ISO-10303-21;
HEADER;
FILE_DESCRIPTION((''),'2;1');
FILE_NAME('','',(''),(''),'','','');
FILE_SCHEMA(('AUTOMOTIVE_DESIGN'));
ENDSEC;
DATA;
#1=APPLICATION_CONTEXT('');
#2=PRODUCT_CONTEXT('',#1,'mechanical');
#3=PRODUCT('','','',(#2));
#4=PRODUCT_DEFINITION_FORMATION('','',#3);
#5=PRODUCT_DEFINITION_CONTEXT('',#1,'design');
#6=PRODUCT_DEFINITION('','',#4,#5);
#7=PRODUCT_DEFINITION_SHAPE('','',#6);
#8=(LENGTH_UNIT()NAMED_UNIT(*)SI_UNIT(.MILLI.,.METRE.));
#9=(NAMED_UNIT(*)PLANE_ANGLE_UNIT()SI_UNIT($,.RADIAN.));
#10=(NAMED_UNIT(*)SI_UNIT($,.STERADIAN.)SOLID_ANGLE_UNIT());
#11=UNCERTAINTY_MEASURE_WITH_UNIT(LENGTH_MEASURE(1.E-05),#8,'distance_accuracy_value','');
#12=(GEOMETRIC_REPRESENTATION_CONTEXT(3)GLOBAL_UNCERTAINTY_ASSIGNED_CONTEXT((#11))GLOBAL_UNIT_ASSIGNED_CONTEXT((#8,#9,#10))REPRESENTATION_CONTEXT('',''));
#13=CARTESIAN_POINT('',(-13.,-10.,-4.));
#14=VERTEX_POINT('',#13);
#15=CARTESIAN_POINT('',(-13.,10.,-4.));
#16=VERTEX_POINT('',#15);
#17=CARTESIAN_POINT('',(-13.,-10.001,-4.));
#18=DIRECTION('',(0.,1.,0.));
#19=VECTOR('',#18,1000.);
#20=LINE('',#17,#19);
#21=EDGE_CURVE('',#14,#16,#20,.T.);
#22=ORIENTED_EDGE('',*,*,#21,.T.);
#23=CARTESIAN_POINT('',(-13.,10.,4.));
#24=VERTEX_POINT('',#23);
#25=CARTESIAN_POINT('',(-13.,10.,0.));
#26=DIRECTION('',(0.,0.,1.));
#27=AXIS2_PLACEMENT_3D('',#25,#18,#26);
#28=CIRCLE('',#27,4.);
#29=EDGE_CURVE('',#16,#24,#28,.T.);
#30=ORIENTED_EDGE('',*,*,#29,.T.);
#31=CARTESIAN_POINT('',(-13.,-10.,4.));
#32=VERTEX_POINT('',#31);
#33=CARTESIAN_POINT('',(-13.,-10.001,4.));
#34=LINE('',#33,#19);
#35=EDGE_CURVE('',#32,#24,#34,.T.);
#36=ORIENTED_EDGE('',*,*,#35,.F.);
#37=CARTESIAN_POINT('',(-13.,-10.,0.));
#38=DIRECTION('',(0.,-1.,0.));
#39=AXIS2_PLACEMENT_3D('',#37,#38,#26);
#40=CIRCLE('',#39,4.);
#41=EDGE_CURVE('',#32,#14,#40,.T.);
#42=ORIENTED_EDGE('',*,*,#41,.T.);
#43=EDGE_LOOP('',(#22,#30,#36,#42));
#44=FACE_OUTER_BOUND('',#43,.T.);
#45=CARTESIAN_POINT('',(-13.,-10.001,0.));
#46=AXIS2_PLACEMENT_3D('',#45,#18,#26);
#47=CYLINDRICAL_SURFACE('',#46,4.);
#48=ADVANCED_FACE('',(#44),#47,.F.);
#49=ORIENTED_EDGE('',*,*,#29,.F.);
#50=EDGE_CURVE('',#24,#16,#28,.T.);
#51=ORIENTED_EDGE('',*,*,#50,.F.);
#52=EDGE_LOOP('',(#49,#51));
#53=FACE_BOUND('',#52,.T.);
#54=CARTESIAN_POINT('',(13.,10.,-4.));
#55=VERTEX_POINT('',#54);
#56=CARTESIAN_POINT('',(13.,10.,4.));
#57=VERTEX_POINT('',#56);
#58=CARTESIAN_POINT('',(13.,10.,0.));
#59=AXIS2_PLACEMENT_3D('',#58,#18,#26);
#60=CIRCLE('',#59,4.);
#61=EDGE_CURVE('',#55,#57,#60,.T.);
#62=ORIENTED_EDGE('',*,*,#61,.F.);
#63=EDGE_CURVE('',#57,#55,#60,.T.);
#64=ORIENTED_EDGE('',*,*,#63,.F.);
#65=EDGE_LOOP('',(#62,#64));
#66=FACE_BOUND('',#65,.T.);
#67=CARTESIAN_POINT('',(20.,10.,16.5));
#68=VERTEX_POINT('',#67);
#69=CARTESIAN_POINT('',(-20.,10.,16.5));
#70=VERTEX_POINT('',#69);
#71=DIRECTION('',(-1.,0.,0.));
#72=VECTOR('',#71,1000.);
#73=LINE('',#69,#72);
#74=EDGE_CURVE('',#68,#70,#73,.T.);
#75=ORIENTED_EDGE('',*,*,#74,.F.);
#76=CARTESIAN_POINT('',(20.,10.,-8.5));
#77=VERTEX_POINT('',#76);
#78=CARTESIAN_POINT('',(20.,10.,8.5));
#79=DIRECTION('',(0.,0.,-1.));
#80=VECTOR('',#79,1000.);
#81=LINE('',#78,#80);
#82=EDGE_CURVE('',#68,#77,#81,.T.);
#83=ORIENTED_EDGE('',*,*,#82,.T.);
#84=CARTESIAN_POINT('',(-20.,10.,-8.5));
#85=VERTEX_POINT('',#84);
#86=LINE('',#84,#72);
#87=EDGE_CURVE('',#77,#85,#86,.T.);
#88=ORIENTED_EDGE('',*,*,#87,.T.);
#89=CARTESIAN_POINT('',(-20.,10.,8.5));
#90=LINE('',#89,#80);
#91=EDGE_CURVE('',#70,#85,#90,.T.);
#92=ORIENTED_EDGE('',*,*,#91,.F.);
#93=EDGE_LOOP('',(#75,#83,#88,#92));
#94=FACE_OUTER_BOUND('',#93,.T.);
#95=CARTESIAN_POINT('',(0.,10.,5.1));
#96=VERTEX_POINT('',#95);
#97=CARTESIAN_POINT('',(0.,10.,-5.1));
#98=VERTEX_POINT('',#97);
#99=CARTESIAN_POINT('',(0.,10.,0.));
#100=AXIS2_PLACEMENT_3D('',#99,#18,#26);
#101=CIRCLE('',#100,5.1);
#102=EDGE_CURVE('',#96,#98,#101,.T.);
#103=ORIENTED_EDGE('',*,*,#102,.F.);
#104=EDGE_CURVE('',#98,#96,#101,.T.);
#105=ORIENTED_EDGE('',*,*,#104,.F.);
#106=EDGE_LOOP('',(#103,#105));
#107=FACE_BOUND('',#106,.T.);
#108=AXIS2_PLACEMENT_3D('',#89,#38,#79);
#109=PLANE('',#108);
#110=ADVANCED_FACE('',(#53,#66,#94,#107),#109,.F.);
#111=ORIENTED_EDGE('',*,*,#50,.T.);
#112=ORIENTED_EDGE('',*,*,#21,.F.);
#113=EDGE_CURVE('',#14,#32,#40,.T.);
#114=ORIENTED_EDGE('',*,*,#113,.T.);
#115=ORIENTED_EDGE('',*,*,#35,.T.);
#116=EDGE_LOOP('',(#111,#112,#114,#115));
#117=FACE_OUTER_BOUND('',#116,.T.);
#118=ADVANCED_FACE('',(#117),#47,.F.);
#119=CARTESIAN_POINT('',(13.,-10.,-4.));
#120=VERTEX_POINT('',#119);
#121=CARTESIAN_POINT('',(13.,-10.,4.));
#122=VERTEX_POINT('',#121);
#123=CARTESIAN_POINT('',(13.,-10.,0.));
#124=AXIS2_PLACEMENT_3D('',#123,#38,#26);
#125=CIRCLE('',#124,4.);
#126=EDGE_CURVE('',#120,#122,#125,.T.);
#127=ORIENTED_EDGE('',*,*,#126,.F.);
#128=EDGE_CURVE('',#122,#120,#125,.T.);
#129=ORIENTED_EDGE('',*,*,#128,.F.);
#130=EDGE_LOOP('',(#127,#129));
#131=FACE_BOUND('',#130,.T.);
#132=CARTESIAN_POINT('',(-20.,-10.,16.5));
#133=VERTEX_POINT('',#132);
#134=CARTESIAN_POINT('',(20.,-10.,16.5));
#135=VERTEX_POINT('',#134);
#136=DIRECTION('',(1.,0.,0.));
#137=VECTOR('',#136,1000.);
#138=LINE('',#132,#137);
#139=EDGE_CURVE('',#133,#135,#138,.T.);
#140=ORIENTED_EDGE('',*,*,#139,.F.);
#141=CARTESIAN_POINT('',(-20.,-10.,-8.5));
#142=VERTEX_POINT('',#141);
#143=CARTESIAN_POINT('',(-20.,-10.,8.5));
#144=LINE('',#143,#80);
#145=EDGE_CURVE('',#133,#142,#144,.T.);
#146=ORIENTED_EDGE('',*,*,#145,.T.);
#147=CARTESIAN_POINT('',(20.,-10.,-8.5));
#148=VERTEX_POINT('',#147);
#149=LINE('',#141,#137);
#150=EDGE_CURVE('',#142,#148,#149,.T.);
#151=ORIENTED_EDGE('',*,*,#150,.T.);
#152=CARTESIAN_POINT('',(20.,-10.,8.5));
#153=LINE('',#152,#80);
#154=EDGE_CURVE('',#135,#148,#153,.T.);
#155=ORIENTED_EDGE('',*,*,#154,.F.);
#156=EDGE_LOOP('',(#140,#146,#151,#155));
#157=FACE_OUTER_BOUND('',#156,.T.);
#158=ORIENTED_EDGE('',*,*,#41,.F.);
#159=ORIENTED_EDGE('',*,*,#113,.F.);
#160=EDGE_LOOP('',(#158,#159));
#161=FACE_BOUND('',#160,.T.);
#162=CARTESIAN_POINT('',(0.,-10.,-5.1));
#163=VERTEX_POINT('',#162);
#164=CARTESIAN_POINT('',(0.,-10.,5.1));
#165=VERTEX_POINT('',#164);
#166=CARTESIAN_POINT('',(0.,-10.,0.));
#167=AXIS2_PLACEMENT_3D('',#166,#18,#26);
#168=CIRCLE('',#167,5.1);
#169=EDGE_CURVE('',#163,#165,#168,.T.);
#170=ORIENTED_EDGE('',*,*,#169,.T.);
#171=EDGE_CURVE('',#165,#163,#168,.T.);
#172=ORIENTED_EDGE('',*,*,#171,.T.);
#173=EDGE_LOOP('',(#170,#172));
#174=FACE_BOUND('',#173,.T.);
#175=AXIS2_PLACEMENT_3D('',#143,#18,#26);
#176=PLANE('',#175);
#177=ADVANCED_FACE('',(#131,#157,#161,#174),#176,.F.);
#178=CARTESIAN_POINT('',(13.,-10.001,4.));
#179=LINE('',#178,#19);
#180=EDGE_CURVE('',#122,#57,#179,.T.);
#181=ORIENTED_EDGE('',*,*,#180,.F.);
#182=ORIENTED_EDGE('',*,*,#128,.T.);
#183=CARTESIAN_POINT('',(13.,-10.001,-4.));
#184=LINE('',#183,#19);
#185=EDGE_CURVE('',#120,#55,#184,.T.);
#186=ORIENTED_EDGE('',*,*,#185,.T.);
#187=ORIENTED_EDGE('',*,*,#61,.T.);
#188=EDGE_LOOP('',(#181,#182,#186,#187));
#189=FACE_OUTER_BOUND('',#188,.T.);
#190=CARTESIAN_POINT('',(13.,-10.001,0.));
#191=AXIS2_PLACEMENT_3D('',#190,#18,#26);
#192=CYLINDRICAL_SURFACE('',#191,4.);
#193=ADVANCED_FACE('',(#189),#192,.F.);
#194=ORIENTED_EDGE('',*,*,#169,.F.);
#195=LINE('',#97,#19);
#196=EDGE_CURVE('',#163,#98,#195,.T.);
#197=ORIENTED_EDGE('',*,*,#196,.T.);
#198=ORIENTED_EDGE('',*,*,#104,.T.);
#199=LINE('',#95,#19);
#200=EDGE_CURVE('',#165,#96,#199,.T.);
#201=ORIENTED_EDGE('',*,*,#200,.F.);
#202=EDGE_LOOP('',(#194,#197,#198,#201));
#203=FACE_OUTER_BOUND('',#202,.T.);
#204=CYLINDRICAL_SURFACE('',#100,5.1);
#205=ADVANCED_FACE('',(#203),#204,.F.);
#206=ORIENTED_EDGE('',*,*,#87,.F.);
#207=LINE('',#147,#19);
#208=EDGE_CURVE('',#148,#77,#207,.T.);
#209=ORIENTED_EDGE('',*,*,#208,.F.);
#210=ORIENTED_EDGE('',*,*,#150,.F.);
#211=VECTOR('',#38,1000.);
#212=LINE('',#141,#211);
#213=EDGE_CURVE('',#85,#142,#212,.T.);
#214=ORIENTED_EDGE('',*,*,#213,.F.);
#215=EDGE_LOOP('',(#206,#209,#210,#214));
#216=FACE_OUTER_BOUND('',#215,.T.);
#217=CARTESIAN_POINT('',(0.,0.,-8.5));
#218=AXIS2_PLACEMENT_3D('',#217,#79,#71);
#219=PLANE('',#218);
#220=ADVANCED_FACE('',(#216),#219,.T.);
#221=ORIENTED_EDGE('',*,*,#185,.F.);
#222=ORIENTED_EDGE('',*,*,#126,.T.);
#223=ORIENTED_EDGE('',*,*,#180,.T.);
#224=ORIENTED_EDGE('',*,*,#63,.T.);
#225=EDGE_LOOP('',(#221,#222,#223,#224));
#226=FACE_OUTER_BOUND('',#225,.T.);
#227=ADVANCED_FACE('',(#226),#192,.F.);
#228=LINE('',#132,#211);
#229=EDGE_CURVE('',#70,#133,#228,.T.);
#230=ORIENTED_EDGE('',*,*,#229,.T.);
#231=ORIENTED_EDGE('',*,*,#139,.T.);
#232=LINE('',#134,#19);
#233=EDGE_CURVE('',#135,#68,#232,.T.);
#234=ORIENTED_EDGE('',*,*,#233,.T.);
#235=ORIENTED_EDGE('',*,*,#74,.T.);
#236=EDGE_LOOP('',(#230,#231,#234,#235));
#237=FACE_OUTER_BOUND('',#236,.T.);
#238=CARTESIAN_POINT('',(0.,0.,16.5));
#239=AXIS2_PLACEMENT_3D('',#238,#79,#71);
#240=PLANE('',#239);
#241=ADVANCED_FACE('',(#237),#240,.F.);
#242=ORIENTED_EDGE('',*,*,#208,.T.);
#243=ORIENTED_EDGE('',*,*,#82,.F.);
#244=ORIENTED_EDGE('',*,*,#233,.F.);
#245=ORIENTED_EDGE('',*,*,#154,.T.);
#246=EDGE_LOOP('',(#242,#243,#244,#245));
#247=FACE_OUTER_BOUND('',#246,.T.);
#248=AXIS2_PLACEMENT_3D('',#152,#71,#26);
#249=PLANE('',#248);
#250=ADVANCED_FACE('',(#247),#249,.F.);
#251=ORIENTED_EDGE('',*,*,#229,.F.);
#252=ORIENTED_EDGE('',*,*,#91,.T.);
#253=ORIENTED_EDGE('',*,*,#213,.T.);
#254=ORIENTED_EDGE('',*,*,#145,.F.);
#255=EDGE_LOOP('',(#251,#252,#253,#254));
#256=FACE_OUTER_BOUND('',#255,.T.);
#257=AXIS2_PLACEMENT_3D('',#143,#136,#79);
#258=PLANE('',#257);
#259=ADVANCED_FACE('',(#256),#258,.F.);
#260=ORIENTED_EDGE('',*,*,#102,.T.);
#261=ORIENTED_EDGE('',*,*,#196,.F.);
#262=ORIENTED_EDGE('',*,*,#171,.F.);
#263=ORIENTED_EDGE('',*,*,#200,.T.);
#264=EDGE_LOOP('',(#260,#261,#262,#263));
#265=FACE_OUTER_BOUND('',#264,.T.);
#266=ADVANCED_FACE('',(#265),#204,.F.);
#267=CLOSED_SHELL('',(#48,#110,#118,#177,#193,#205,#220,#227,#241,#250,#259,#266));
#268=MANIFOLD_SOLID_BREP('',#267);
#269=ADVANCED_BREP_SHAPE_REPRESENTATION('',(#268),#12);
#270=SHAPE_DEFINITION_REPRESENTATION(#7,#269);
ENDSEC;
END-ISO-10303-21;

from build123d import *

# Parameters (mm, degrees)
SKETCH_1_W              = 40
SKETCH_1_H              = 20
EXTRUDE_1_DEPTH         = 8.5
CUT_EXTRUDE_1_REACH     = 31.534
SKETCH_2_R              = 4
CUT_EXTRUDE_2_REACH     = 31.534
SKETCH_3_R              = 4
SKETCH_6_W              = 40
SKETCH_6_H              = 20
EXTRUDE_3_DEPTH         = 8
HOLE_WIZARD_M12_1_D     = 10.2
HOLE_WIZARD_M12_1_DEPTH = 20


with BuildPart() as part:
    # 草图1 → 凸台-拉伸1 (new, symmetric)
    with BuildSketch(Plane.XY):
        Rectangle(SKETCH_1_W, SKETCH_1_H)
    extrude(amount=EXTRUDE_1_DEPTH, both=True)

    # 草图2 → 切除-拉伸1 (cut, up to next)
    with BuildSketch(Plane(origin=(0, 10, 0), x_dir=(1, 0, 0), z_dir=(0, 1, 0)), mode=Mode.PRIVATE) as cut_extrude_1_sk1:
        with Locations(Location((-13, 0, 0), (0, 0, 270))):
            Circle(SKETCH_2_R)
    cut_extrude_1_tool1 = extrude(cut_extrude_1_sk1.sketch, amount=-CUT_EXTRUDE_1_REACH, mode=Mode.PRIVATE) & part.part
    # 草图2 → 切除-拉伸1 (cut, up to next)
    with BuildSketch(Plane(origin=(0, 10, 0), x_dir=(1, 0, 0), z_dir=(0, 1, 0)), mode=Mode.PRIVATE) as cut_extrude_1_sk2:
        with Locations(Location((13, 0, 0), (0, 0, 270))):
            Circle(SKETCH_2_R)
    cut_extrude_1_tool2 = extrude(cut_extrude_1_sk2.sketch, amount=-CUT_EXTRUDE_1_REACH, mode=Mode.PRIVATE) & part.part
    add(cut_extrude_1_tool1.solids().sort_by_distance((-13, 10, 0))[0], mode=Mode.SUBTRACT)
    add(cut_extrude_1_tool2.solids().sort_by_distance((13, 10, 0))[0], mode=Mode.SUBTRACT)

    # 草图3 → 切除-拉伸2 (cut, up to next)
    with BuildSketch(Plane.XZ.offset(10), mode=Mode.PRIVATE) as cut_extrude_2_sk1:
        with Locations(Location((0, 0, 0), (0, 0, 270))):
            Circle(SKETCH_3_R)
    cut_extrude_2_tool1 = extrude(cut_extrude_2_sk1.sketch, amount=-CUT_EXTRUDE_2_REACH, mode=Mode.PRIVATE) & part.part
    add(cut_extrude_2_tool1.solids().sort_by_distance((0, -10, 0))[0], mode=Mode.SUBTRACT)

    # 草图6 → 凸台-拉伸3 (add)
    with BuildSketch(Plane.XY.offset(8.5)):
        Rectangle(SKETCH_6_W, SKETCH_6_H)
    extrude(amount=EXTRUDE_3_DEPTH)

    # M12 螺纹孔1
    with Locations(Plane.ZX.offset(10)):
        with Locations((0, 0)):
            Hole(HOLE_WIZARD_M12_1_D / 2, depth=HOLE_WIZARD_M12_1_DEPTH)


solid = part.part
